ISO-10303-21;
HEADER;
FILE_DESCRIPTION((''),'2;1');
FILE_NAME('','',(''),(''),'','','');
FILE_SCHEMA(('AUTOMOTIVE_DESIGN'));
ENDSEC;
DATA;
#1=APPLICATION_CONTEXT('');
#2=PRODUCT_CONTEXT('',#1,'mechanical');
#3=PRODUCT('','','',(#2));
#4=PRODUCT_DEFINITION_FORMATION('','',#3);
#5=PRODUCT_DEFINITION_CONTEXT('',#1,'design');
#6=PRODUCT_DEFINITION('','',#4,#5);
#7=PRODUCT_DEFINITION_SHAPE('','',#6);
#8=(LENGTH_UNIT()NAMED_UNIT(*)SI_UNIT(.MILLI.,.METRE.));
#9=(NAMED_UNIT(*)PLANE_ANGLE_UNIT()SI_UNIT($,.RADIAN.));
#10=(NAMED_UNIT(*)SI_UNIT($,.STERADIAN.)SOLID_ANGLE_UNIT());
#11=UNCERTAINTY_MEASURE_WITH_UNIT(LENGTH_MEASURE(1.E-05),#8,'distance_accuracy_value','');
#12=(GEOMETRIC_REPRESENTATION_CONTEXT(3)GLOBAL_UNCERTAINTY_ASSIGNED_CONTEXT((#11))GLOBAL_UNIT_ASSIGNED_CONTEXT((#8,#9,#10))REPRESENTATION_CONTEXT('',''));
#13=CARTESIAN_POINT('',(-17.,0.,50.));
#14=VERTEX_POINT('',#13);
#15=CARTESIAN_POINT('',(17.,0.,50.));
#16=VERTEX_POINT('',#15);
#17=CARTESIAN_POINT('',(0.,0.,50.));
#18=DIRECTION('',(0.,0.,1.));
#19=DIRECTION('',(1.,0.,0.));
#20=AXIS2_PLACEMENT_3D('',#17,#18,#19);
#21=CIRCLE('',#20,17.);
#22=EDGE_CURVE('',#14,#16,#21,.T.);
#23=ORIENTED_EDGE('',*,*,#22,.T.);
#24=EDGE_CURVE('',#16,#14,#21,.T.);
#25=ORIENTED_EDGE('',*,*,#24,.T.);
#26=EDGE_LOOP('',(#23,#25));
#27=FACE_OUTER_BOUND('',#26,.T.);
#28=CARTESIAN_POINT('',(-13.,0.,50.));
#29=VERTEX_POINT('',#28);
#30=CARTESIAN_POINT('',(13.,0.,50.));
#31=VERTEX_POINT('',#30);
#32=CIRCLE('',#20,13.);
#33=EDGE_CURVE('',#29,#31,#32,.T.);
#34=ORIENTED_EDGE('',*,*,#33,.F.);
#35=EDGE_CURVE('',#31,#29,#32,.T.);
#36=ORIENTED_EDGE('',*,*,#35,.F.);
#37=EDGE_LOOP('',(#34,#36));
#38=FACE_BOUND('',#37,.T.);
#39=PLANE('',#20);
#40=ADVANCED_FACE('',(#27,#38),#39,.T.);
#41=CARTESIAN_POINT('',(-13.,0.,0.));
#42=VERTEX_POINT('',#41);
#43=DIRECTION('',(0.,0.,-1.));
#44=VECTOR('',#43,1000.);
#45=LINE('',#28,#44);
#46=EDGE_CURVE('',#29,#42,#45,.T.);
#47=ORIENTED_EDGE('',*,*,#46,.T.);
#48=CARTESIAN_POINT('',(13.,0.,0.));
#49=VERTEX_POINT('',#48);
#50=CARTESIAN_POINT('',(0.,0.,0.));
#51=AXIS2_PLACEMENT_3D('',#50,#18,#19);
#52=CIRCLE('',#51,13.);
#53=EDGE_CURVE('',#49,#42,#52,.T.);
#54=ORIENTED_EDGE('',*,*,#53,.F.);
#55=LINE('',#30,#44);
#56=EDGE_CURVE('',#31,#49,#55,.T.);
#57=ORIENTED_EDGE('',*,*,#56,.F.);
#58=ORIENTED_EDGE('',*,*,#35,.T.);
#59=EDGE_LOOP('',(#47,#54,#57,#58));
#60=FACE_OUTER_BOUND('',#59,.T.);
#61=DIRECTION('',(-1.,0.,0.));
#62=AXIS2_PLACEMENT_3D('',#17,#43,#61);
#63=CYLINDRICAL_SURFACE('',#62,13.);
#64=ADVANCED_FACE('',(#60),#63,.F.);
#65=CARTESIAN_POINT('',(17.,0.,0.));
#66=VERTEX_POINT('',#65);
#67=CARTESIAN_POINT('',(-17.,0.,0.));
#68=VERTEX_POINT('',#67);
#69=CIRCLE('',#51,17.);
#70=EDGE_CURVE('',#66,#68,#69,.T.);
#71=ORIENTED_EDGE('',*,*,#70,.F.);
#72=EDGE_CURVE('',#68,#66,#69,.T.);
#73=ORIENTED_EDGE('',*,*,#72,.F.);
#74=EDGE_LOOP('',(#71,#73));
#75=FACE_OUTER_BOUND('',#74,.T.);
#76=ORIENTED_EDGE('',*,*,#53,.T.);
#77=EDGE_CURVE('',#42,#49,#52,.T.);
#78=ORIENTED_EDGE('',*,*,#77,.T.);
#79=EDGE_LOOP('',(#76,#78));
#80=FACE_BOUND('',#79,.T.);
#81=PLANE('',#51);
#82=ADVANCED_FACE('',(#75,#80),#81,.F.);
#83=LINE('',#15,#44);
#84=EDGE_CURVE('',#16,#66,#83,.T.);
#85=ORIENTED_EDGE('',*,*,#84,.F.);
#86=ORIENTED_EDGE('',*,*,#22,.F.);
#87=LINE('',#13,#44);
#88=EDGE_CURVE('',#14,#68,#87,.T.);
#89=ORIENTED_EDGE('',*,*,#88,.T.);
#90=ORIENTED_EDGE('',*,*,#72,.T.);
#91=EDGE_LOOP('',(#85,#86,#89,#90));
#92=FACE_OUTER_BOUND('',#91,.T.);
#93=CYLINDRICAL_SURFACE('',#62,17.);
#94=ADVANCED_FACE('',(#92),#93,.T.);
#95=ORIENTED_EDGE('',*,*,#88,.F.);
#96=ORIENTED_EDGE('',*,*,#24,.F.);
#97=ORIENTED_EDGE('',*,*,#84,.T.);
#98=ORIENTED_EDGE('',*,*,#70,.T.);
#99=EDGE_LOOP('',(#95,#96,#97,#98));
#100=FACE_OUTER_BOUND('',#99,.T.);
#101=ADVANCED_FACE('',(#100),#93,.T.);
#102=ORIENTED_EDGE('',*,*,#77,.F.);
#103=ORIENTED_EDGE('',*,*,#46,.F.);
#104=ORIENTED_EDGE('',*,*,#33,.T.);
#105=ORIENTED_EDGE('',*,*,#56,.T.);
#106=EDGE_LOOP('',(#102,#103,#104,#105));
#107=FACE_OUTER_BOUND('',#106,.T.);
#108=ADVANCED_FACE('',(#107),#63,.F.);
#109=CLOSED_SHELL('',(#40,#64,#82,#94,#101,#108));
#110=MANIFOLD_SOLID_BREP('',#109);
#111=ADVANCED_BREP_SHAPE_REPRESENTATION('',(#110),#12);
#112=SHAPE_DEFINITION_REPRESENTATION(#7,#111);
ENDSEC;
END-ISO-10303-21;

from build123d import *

# Parameters (mm, degrees)
SKETCH1_R           = 17
SKETCH1_R_2         = 13
BOSS_EXTRUDE1_DEPTH = 50


with BuildPart() as part:
    # Sketch1 → Boss-Extrude1 (new body)
    with BuildSketch(Plane.XY):
        Circle(SKETCH1_R)
        Circle(SKETCH1_R_2, mode=Mode.SUBTRACT)
    extrude(amount=BOSS_EXTRUDE1_DEPTH)


solid = part.part
